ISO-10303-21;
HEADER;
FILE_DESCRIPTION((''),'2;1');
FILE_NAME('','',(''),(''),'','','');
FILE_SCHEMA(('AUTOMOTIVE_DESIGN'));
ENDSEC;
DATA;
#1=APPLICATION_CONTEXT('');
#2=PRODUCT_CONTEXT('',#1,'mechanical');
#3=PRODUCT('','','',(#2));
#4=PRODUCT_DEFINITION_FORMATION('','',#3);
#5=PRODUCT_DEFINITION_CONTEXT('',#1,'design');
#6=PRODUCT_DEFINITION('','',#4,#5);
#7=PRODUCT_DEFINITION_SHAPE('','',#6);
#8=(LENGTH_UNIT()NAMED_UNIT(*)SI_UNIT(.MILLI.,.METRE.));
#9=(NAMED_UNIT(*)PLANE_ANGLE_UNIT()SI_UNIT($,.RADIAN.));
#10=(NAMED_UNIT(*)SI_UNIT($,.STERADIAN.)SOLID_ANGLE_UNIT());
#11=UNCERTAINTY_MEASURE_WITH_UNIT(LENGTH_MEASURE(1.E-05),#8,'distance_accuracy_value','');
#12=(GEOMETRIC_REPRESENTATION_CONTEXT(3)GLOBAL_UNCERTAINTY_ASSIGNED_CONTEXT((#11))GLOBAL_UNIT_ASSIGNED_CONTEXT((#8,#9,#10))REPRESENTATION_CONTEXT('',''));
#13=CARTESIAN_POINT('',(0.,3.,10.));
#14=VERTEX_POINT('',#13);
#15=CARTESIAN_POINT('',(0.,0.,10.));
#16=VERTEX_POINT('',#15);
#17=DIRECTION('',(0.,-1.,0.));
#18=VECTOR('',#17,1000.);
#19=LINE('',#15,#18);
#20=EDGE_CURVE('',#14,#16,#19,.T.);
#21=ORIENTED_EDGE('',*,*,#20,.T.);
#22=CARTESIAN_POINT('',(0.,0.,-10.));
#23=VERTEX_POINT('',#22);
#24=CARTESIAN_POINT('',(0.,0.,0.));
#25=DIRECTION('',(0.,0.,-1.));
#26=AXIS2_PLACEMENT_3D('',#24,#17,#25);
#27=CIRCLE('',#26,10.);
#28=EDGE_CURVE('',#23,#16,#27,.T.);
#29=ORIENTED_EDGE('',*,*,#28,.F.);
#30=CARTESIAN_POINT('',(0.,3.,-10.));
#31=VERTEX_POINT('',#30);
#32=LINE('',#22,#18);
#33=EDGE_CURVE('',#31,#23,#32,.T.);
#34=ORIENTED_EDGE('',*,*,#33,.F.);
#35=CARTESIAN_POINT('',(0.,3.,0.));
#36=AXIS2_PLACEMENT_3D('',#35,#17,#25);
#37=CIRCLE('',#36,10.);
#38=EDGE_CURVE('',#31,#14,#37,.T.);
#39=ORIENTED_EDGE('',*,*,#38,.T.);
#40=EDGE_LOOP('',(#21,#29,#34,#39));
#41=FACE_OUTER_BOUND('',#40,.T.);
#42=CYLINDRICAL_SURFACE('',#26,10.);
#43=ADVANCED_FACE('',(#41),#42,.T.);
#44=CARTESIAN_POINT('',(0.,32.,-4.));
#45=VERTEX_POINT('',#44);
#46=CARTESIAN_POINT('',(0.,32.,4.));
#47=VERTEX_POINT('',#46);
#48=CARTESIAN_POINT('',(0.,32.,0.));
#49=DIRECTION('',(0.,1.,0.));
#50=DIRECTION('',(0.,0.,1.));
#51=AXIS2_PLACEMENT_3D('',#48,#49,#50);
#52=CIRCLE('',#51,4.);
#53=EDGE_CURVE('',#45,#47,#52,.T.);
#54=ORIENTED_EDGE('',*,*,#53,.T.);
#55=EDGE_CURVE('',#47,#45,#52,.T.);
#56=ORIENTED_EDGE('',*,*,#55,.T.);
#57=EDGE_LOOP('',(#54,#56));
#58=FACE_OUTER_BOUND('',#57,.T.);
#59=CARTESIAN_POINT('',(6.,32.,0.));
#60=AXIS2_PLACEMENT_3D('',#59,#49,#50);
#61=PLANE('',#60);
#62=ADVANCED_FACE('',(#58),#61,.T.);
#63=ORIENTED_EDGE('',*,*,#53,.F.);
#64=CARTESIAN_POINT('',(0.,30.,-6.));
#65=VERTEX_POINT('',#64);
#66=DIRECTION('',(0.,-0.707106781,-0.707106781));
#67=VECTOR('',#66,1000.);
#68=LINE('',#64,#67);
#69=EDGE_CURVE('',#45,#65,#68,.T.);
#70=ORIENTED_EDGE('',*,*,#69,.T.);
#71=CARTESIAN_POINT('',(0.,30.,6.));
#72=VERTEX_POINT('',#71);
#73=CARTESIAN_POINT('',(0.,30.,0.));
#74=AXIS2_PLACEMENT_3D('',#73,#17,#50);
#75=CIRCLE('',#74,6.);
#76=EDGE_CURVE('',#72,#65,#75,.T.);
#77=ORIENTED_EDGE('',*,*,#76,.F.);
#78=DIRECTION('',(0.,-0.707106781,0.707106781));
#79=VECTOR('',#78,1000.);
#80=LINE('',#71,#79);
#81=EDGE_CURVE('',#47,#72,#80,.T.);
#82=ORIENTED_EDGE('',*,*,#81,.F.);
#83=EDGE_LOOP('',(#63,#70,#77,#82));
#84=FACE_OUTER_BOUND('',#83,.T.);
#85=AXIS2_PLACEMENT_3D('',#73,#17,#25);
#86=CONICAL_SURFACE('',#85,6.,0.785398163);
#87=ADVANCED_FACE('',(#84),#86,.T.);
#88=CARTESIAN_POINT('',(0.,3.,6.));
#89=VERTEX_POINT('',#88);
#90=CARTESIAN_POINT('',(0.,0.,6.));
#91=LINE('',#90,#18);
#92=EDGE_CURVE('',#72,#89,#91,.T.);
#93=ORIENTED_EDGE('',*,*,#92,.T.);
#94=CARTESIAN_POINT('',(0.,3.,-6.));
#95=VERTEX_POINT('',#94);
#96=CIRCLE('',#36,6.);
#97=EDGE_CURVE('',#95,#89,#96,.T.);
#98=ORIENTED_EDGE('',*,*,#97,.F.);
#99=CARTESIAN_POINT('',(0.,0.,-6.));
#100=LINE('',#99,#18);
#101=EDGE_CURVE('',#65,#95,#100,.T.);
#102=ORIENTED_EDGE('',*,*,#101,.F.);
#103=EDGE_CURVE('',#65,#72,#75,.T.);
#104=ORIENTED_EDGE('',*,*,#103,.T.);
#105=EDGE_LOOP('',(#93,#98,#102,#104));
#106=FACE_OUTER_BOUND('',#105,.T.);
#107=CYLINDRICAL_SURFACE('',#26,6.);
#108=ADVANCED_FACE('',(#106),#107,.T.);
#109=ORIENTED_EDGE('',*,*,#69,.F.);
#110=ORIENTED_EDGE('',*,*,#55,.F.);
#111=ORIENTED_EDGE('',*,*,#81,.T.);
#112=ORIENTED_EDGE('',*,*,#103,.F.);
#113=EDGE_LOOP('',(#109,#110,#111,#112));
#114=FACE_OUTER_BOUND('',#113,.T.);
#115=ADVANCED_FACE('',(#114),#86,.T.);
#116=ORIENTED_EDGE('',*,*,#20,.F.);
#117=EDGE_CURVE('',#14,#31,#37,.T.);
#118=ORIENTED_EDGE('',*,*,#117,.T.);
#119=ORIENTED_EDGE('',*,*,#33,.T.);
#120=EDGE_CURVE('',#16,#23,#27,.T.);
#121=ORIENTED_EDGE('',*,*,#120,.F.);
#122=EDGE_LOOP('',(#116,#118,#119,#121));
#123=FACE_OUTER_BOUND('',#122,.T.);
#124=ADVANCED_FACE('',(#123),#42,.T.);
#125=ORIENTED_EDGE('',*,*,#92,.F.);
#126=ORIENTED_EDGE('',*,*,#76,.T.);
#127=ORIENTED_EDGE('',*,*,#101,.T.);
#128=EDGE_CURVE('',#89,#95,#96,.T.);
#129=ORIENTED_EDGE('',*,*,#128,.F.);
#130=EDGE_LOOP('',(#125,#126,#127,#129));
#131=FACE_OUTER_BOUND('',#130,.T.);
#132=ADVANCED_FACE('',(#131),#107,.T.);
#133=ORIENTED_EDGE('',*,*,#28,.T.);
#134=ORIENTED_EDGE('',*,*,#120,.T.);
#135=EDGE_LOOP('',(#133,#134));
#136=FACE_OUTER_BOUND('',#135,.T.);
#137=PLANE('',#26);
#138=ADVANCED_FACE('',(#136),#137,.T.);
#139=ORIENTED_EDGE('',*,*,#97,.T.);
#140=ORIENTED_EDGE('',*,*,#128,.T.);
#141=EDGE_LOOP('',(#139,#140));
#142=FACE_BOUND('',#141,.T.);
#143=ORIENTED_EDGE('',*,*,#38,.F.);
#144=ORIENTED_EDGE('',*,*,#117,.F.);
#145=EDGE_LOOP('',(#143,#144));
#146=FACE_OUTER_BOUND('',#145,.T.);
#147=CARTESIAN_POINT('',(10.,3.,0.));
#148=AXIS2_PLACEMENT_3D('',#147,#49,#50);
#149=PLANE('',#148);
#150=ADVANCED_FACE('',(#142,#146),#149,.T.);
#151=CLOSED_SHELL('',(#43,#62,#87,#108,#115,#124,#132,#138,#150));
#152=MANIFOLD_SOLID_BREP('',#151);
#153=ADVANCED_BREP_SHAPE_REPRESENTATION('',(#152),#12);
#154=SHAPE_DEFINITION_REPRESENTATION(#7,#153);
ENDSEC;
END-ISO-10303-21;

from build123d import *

# Parameters (mm, degrees)
CHAMFER1_SIZE = 2


with BuildPart() as part:
    # Sketch1 → Revolve1 (revolve)
    with BuildSketch(Plane.XY, mode=Mode.PRIVATE) as revolve1_sk:
        Polygon((0, 0), (10, 0), (10, 3), (6, 3), (6, 32), (0, 32), align=None)
    revolve(revolve1_sk.sketch.rotate(Axis((0, 0, 0), (0, 1, 0)), 90), axis=Axis((0, 0, 0), (0, 1, 0)))

    # Chamfer1
    chamfer1_edges = [part.edges().sort_by_distance(p)[0] for p in [
        (0, 32, 6),
    ]]
    chamfer(chamfer1_edges, length=CHAMFER1_SIZE)


solid = part.part
